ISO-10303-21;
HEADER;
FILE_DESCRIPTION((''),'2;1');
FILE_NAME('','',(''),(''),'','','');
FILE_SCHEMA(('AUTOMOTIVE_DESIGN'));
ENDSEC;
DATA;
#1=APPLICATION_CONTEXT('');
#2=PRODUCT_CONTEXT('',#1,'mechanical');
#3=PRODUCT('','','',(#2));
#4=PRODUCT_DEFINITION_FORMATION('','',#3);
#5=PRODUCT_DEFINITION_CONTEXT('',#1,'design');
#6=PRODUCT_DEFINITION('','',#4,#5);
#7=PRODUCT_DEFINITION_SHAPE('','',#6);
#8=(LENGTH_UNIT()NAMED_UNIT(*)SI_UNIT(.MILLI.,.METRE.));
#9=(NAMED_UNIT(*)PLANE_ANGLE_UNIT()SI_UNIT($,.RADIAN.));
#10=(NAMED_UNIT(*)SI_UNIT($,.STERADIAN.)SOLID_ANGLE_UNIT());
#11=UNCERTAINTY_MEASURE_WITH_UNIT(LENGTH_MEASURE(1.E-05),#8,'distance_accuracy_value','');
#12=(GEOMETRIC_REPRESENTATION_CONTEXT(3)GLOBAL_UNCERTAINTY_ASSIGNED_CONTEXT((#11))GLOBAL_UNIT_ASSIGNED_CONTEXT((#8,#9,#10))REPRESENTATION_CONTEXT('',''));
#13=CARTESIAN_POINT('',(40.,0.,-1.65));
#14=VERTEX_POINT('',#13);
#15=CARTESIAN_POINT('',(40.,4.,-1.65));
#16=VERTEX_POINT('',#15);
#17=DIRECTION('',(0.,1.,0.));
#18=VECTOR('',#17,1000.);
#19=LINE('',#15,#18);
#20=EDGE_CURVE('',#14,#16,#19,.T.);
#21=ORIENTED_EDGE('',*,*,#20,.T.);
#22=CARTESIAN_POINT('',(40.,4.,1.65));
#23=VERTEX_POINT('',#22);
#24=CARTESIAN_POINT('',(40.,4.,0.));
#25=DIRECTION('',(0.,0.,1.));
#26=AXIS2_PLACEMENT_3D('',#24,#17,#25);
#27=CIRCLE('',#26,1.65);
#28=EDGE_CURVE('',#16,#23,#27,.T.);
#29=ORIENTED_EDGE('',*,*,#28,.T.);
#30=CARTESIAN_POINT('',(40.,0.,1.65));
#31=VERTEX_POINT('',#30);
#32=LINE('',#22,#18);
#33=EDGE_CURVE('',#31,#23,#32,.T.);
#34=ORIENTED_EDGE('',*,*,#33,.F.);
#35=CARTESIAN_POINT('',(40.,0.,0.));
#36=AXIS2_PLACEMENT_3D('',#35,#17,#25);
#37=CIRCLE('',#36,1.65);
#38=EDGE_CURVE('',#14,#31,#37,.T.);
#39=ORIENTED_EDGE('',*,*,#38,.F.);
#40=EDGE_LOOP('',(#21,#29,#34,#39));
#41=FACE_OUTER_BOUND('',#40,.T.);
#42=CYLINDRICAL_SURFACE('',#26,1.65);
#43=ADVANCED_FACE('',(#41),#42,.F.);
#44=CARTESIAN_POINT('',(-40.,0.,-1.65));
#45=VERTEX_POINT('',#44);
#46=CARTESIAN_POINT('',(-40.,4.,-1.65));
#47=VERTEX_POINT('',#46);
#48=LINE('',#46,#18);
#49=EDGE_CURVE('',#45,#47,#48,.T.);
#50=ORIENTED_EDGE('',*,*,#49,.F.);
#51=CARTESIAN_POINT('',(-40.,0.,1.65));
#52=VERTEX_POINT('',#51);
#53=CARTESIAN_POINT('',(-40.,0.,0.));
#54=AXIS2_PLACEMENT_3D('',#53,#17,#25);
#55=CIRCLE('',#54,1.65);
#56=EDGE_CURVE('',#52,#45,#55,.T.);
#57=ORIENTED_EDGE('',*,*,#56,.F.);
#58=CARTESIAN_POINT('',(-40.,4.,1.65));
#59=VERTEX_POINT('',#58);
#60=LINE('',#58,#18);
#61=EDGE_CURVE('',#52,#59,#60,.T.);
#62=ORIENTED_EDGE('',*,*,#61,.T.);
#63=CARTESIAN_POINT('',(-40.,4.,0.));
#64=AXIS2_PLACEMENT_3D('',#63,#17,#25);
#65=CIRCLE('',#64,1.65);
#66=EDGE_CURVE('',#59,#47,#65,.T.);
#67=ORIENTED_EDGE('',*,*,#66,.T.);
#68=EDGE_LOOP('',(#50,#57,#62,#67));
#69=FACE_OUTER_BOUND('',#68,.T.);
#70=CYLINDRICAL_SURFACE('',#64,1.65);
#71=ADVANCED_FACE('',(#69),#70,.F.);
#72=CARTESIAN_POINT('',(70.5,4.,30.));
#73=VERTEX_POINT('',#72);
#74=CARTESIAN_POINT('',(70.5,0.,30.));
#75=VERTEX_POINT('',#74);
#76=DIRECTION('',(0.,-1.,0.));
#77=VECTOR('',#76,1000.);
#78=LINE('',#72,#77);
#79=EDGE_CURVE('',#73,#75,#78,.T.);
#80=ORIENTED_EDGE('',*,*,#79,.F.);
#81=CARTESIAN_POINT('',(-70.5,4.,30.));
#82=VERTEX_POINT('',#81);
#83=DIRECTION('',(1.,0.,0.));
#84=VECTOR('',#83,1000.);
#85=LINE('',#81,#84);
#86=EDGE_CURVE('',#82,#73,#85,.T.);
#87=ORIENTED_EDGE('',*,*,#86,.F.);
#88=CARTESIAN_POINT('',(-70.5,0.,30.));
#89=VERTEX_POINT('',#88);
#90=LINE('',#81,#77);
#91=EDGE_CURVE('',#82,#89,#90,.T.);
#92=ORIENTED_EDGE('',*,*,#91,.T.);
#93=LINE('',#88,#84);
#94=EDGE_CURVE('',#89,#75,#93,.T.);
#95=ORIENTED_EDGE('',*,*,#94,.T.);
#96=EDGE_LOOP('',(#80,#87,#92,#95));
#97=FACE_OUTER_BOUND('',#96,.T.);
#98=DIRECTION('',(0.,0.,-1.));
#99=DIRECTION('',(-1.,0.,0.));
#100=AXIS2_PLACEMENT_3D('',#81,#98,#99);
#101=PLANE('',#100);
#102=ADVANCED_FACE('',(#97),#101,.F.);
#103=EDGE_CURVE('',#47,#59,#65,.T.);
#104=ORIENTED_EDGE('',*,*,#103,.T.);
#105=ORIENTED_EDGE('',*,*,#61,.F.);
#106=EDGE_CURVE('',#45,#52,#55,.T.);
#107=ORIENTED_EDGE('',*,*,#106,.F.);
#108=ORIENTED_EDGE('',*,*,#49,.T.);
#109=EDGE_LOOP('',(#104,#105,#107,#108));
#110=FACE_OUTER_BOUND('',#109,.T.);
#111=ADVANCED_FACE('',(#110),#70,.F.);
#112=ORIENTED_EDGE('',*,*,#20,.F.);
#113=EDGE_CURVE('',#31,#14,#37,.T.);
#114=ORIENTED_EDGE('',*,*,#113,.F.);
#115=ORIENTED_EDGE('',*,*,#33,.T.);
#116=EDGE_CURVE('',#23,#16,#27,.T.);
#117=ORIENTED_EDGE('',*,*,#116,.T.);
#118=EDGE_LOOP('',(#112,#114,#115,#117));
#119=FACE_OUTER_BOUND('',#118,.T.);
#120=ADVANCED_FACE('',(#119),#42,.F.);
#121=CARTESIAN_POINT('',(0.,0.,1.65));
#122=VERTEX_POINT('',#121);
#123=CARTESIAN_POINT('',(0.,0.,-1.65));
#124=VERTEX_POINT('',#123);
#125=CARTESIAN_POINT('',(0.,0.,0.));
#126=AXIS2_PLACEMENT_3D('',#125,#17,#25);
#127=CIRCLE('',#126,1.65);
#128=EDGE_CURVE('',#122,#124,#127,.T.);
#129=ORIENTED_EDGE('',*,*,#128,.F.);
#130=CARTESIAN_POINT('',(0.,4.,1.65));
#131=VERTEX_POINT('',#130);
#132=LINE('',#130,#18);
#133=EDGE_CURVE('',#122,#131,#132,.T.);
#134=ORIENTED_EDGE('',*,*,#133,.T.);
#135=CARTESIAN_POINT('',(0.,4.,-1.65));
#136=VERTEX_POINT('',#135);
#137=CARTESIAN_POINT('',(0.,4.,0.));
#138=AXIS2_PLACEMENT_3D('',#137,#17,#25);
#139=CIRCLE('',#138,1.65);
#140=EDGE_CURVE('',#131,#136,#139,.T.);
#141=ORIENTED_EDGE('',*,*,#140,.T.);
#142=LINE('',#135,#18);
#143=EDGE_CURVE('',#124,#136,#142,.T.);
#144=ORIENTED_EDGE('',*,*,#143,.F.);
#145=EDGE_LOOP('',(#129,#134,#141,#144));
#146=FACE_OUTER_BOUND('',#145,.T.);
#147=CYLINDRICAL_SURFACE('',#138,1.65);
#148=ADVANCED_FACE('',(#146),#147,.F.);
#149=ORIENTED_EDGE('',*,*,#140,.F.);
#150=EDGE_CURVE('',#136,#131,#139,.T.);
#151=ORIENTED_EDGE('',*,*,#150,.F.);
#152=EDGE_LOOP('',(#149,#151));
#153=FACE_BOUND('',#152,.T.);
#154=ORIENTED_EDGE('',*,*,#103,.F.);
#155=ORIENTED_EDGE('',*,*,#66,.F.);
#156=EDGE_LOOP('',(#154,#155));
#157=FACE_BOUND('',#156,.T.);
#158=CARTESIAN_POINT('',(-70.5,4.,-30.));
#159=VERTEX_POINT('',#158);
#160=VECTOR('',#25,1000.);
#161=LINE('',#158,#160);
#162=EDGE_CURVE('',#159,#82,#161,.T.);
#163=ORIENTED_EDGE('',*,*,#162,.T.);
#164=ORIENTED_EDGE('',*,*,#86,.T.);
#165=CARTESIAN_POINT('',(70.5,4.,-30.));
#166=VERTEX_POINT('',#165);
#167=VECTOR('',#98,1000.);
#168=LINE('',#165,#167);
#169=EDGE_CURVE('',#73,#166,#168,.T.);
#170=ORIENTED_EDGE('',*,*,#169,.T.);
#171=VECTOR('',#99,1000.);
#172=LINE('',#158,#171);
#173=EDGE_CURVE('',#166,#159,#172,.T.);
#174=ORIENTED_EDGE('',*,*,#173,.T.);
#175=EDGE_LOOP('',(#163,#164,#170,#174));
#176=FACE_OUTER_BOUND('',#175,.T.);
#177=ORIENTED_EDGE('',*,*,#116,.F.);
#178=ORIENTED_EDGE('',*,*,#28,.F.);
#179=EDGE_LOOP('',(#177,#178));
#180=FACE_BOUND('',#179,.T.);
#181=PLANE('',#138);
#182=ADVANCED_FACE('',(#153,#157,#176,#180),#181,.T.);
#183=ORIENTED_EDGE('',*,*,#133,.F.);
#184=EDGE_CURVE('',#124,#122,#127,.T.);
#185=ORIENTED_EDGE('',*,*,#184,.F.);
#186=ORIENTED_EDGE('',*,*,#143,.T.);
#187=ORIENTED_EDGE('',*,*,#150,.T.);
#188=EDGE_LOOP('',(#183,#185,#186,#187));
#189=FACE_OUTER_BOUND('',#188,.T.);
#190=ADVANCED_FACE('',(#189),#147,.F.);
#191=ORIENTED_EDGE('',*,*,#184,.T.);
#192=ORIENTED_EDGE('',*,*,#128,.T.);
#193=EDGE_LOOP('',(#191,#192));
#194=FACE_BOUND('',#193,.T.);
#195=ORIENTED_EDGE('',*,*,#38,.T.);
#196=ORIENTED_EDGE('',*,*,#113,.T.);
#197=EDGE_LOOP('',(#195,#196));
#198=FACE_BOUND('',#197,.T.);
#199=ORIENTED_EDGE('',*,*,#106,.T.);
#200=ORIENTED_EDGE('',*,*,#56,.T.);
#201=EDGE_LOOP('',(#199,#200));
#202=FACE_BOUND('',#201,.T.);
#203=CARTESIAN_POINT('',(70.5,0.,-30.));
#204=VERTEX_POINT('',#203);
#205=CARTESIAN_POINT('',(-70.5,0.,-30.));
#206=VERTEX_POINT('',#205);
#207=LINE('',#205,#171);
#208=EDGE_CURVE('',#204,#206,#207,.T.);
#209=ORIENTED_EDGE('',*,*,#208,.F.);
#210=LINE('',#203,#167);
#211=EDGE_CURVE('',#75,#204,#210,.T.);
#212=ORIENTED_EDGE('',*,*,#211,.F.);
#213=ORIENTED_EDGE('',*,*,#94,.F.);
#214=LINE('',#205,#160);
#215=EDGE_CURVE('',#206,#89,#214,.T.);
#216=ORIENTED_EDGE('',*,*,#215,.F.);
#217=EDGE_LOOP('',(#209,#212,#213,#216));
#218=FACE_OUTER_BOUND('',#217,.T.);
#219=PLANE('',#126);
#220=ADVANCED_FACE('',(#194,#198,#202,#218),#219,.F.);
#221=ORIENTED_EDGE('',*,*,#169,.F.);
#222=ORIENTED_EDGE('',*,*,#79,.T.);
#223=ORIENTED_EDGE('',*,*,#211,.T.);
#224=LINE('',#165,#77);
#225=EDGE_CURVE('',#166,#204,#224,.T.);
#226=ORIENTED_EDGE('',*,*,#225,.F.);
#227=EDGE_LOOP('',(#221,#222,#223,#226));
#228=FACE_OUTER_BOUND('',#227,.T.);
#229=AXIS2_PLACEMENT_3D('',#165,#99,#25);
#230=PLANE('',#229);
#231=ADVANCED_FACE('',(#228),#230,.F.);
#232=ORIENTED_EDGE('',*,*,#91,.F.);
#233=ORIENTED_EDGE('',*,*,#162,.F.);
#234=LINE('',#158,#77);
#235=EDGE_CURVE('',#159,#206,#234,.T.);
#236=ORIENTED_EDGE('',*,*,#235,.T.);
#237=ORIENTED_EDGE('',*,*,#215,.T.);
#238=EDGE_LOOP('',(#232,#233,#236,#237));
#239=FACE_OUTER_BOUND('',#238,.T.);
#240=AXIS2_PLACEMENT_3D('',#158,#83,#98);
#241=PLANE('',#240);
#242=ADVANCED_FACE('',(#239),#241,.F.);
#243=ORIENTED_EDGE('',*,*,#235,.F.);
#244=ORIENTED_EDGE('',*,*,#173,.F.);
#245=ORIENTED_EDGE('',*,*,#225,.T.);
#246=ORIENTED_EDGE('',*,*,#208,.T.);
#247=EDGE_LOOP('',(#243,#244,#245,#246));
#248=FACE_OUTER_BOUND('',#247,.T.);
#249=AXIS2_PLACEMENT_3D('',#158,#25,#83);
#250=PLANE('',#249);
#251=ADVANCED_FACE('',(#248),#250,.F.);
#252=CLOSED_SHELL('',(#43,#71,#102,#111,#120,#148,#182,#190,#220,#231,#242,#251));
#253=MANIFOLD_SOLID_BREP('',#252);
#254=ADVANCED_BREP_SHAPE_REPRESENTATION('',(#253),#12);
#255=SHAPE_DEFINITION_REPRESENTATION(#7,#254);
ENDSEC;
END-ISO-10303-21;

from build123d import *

# Parameters (mm, degrees)
SKETCH1_W           = 141
SKETCH1_H           = 60
BOSS_EXTRUDE1_DEPTH = 4
M4_TAPPED_HOLE1_D   = 3.3


with BuildPart() as part:
    # Sketch1 → Boss-Extrude1 (new body)
    with BuildSketch(Plane(origin=(0, 0, 0), x_dir=(1, 0, 0), z_dir=(0, 1, 0))):
        Rectangle(SKETCH1_W, SKETCH1_H)
    extrude(amount=BOSS_EXTRUDE1_DEPTH)

    # M4 Tapped Hole1 (through all)
    with Locations(Plane(origin=(0, 4, 0), x_dir=(1, 0, 0), z_dir=(0, 1, 0))):
        with Locations((-40, 0), (0, 0), (40, 0)):
            Hole(M4_TAPPED_HOLE1_D / 2)


solid = part.part
